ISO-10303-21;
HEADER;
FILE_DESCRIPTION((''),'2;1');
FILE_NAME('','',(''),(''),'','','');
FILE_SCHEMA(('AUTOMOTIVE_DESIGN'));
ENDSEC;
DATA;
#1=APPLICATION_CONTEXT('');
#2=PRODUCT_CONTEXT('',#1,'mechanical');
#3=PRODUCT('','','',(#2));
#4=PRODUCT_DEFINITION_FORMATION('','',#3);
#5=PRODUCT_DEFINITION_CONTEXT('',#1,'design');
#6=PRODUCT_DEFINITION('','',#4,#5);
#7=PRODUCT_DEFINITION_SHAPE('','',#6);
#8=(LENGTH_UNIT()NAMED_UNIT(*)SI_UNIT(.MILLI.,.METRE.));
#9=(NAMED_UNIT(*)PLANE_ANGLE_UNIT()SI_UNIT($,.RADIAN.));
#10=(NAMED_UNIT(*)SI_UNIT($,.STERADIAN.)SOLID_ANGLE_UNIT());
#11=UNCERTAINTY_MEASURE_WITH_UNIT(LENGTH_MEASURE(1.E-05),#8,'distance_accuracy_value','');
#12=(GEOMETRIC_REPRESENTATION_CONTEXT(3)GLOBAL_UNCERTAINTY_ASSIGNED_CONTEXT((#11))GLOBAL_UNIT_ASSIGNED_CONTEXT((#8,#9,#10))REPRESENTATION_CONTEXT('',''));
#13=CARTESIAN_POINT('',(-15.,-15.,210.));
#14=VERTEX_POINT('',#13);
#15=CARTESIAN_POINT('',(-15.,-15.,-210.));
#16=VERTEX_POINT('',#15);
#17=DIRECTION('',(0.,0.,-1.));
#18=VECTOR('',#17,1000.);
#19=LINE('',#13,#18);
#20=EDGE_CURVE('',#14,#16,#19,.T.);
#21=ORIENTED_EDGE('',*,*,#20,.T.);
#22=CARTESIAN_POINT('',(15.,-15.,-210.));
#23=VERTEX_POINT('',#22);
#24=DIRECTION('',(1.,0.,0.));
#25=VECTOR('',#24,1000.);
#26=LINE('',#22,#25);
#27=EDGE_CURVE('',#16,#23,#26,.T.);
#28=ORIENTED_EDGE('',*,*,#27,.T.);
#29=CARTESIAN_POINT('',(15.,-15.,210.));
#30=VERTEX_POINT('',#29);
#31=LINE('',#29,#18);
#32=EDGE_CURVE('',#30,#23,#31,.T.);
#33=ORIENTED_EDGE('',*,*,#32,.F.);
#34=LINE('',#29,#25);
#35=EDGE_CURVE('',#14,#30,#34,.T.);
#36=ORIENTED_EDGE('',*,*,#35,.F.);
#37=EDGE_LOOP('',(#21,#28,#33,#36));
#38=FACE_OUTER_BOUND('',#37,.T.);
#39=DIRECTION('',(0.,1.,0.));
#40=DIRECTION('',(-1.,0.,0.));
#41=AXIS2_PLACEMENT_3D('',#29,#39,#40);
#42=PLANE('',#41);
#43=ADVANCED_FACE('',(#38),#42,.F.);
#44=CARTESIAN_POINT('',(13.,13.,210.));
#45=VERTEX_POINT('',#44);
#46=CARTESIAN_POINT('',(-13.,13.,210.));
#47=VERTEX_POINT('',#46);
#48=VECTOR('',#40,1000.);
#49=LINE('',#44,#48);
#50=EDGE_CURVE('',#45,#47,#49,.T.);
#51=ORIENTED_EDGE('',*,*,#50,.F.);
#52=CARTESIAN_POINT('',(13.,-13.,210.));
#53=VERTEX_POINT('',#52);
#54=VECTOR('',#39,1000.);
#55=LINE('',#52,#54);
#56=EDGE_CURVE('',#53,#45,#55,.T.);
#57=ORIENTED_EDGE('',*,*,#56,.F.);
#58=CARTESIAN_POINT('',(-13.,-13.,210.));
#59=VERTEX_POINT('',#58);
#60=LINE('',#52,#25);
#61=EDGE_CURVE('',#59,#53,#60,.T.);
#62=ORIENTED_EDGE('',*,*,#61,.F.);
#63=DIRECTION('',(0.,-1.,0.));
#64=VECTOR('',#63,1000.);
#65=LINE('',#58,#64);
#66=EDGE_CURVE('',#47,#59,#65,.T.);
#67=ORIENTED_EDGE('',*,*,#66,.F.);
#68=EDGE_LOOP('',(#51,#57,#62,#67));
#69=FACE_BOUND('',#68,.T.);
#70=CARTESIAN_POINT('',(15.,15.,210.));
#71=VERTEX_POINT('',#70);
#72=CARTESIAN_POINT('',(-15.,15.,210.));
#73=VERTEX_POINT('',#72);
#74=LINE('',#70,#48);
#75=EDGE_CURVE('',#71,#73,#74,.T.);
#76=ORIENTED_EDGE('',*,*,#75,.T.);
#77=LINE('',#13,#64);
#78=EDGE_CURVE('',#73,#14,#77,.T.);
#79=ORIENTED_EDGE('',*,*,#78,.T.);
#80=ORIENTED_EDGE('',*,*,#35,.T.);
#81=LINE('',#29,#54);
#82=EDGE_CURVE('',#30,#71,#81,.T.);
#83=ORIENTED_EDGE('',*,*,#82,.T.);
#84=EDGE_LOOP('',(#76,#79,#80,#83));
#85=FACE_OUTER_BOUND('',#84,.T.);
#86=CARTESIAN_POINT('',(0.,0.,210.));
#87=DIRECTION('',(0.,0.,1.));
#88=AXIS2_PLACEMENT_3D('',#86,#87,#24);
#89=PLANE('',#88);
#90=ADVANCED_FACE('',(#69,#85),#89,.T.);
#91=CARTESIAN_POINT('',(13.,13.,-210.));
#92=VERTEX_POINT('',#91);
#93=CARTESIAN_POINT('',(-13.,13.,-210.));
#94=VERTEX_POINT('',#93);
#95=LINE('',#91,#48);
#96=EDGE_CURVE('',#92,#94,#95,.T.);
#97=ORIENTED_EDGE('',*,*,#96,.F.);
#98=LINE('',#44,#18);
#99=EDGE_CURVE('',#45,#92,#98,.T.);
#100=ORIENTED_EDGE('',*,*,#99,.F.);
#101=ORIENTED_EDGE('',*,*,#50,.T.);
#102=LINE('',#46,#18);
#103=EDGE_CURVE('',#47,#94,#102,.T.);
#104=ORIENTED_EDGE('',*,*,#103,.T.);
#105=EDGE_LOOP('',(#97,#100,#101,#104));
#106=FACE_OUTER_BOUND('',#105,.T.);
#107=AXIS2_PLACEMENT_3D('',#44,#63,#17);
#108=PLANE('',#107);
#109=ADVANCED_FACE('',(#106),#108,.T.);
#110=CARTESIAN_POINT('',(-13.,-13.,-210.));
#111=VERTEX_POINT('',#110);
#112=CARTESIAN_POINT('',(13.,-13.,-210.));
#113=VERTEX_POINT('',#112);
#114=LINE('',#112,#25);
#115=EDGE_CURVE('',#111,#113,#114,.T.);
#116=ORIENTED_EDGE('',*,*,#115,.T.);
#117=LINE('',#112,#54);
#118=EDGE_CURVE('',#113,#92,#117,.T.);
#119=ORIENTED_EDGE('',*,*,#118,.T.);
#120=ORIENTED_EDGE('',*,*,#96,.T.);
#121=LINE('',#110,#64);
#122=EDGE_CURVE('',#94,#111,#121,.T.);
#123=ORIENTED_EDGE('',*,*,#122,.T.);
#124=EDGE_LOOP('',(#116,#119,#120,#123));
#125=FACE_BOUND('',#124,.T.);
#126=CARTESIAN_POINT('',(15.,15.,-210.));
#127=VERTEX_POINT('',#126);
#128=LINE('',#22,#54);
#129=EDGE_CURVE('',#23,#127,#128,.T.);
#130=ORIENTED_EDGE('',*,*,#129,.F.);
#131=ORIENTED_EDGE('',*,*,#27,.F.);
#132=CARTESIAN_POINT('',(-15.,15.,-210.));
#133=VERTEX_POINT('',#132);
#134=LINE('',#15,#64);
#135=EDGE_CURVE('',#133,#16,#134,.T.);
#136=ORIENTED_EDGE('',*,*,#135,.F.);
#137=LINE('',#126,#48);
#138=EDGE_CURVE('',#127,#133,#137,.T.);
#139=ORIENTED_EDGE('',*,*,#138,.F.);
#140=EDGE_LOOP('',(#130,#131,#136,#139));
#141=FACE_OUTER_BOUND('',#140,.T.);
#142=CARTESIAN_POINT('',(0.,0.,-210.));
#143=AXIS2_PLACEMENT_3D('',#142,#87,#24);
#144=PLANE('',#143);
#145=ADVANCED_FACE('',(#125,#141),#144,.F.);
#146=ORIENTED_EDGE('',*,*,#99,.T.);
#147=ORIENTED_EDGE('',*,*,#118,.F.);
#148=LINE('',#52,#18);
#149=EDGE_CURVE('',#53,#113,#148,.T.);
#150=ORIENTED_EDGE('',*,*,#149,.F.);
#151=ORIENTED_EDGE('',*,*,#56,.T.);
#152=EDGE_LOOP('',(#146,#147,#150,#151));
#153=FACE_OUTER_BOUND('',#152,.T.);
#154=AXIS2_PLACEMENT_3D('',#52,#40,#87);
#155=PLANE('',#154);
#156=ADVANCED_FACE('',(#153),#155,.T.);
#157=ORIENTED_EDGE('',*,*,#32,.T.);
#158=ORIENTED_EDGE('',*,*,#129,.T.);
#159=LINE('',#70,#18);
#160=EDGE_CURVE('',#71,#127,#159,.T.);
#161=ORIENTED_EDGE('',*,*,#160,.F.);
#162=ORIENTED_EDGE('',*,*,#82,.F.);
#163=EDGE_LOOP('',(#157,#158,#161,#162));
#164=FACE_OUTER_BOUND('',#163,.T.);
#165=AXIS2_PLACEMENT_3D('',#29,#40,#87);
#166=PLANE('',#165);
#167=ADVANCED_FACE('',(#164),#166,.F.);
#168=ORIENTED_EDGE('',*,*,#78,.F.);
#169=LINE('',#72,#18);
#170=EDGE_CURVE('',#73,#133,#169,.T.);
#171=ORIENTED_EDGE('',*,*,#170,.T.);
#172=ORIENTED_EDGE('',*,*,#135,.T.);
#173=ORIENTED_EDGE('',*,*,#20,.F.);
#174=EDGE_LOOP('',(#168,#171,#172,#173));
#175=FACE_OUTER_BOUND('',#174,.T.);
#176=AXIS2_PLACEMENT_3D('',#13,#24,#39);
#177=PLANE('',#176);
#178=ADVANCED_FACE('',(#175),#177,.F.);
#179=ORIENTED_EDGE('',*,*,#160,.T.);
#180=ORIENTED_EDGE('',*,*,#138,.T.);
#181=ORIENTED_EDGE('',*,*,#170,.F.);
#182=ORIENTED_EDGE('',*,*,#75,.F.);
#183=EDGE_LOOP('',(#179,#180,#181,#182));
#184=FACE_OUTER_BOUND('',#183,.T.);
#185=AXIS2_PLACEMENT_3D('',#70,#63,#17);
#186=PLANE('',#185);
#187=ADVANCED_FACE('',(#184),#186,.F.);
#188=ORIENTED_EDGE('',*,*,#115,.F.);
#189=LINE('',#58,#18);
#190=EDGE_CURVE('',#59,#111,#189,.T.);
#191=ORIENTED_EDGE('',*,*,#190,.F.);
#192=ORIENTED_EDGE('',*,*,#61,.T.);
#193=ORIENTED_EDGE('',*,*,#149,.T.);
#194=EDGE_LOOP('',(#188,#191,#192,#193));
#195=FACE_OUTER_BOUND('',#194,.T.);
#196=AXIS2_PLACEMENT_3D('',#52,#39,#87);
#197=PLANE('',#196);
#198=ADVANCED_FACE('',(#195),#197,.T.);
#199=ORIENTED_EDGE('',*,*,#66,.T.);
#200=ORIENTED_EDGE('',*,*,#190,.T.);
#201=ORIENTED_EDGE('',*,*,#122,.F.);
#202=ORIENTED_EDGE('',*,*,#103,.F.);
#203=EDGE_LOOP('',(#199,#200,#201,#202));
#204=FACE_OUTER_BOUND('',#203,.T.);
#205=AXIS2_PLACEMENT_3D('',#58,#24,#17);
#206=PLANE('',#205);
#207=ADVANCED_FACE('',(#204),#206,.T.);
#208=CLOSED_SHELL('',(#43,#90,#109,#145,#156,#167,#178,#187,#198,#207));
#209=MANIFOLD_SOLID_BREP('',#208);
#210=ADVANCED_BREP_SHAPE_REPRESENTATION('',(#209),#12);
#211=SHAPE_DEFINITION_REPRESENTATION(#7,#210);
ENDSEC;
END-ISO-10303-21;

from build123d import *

# Parameters (mm, degrees)
SKETCH_1_W      = 30
SKETCH_1_H      = 30
SKETCH_1_W_2    = 26
SKETCH_1_H_2    = 26
EXTRUDE_1_DEPTH = 210


with BuildPart() as part:
    # 草图1 → 凸台-拉伸1 (new, symmetric)
    with BuildSketch(Plane.XY):
        Rectangle(SKETCH_1_W, SKETCH_1_H)
        Rectangle(SKETCH_1_W_2, SKETCH_1_H_2, mode=Mode.SUBTRACT)
    extrude(amount=EXTRUDE_1_DEPTH, both=True)


solid = part.part
